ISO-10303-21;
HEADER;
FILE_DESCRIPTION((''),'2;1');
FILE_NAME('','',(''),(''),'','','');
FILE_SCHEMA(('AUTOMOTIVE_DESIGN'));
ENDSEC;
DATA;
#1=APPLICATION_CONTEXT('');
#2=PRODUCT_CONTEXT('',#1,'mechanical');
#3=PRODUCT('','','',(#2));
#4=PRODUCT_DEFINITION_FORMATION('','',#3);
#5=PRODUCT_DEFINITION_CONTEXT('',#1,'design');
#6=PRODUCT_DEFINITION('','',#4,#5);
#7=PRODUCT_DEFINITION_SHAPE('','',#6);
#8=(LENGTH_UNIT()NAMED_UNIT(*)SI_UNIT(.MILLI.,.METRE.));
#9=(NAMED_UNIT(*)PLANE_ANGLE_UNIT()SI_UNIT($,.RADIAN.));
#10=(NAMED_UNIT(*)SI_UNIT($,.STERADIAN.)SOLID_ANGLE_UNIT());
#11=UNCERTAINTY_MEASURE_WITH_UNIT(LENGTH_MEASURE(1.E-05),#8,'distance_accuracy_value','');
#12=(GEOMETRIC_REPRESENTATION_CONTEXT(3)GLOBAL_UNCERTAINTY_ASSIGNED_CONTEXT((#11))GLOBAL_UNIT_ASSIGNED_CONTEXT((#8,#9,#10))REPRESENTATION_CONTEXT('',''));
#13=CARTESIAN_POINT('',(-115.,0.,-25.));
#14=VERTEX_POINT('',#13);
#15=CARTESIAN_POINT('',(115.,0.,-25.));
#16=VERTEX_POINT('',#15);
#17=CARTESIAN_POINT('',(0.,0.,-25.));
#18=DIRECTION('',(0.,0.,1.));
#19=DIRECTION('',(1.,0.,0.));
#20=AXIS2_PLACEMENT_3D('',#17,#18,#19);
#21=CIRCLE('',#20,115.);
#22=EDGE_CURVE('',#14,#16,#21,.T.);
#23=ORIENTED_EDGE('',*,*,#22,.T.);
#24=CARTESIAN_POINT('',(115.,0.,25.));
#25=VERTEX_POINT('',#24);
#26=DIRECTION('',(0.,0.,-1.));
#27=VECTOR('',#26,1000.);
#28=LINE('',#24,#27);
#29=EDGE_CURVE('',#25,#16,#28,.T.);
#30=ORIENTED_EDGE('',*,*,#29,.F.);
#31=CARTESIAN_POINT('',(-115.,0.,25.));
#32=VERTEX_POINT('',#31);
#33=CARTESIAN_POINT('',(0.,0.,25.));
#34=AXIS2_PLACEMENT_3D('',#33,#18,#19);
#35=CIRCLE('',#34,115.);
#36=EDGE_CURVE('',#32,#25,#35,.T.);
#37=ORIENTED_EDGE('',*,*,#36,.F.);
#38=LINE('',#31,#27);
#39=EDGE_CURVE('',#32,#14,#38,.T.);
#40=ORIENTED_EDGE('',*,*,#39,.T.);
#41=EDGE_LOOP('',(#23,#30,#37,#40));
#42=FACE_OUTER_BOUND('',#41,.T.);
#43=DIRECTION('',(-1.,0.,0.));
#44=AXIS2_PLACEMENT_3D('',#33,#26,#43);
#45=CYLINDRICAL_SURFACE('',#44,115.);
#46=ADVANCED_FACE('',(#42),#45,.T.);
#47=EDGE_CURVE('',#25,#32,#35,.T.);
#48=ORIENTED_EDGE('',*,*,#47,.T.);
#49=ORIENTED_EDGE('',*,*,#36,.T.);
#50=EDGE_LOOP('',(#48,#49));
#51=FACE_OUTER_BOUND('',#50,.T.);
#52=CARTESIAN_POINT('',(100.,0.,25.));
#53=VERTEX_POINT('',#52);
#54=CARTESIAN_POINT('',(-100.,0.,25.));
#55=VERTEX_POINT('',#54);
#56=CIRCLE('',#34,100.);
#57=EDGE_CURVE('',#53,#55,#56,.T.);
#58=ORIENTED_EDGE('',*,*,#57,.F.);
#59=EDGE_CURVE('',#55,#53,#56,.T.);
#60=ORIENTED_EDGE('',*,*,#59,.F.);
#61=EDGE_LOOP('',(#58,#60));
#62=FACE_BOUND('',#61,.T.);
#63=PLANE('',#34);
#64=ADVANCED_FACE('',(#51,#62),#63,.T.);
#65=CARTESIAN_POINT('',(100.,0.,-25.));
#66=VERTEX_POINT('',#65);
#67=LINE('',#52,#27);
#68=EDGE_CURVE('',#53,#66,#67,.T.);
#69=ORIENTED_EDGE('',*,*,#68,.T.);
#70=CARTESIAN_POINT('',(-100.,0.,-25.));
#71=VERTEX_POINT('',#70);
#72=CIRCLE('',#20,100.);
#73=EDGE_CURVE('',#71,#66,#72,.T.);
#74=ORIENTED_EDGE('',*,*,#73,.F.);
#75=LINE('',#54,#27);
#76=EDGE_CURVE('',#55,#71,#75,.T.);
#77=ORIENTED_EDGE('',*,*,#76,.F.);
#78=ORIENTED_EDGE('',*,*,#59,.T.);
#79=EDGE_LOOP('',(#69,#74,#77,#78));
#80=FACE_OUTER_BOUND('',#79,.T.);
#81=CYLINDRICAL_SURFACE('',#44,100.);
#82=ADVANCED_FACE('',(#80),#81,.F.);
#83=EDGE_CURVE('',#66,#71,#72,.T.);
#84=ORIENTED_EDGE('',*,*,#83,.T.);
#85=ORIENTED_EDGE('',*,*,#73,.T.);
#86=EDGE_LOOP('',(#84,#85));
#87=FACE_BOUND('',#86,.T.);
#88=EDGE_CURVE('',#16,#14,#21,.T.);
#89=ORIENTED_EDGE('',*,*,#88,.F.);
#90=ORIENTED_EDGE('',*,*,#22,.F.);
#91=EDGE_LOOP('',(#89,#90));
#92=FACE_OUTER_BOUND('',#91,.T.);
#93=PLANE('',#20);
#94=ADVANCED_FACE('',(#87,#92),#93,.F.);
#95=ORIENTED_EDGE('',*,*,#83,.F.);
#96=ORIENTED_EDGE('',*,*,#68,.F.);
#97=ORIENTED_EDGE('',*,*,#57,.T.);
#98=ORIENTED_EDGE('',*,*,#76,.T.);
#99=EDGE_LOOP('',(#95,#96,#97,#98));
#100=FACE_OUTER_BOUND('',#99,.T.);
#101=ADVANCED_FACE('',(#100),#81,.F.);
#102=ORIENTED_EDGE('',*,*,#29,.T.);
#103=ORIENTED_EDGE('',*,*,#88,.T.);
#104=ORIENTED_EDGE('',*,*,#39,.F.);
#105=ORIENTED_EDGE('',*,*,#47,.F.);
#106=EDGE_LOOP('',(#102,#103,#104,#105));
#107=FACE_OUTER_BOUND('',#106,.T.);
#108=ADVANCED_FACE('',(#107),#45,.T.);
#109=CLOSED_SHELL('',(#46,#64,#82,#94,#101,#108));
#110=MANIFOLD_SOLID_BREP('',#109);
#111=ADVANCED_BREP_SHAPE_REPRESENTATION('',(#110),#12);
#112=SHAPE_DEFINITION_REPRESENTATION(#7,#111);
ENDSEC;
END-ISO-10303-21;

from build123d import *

# Parameters (mm, degrees)
SKETCH1_R           = 115
SKETCH1_R_2         = 100
BOSS_EXTRUDE1_DEPTH = 25


with BuildPart() as part:
    # Sketch1 → Boss-Extrude1 (new, symmetric)
    with BuildSketch(Plane.XY):
        Circle(SKETCH1_R)
        Circle(SKETCH1_R_2, mode=Mode.SUBTRACT)
    extrude(amount=BOSS_EXTRUDE1_DEPTH, both=True)


solid = part.part
